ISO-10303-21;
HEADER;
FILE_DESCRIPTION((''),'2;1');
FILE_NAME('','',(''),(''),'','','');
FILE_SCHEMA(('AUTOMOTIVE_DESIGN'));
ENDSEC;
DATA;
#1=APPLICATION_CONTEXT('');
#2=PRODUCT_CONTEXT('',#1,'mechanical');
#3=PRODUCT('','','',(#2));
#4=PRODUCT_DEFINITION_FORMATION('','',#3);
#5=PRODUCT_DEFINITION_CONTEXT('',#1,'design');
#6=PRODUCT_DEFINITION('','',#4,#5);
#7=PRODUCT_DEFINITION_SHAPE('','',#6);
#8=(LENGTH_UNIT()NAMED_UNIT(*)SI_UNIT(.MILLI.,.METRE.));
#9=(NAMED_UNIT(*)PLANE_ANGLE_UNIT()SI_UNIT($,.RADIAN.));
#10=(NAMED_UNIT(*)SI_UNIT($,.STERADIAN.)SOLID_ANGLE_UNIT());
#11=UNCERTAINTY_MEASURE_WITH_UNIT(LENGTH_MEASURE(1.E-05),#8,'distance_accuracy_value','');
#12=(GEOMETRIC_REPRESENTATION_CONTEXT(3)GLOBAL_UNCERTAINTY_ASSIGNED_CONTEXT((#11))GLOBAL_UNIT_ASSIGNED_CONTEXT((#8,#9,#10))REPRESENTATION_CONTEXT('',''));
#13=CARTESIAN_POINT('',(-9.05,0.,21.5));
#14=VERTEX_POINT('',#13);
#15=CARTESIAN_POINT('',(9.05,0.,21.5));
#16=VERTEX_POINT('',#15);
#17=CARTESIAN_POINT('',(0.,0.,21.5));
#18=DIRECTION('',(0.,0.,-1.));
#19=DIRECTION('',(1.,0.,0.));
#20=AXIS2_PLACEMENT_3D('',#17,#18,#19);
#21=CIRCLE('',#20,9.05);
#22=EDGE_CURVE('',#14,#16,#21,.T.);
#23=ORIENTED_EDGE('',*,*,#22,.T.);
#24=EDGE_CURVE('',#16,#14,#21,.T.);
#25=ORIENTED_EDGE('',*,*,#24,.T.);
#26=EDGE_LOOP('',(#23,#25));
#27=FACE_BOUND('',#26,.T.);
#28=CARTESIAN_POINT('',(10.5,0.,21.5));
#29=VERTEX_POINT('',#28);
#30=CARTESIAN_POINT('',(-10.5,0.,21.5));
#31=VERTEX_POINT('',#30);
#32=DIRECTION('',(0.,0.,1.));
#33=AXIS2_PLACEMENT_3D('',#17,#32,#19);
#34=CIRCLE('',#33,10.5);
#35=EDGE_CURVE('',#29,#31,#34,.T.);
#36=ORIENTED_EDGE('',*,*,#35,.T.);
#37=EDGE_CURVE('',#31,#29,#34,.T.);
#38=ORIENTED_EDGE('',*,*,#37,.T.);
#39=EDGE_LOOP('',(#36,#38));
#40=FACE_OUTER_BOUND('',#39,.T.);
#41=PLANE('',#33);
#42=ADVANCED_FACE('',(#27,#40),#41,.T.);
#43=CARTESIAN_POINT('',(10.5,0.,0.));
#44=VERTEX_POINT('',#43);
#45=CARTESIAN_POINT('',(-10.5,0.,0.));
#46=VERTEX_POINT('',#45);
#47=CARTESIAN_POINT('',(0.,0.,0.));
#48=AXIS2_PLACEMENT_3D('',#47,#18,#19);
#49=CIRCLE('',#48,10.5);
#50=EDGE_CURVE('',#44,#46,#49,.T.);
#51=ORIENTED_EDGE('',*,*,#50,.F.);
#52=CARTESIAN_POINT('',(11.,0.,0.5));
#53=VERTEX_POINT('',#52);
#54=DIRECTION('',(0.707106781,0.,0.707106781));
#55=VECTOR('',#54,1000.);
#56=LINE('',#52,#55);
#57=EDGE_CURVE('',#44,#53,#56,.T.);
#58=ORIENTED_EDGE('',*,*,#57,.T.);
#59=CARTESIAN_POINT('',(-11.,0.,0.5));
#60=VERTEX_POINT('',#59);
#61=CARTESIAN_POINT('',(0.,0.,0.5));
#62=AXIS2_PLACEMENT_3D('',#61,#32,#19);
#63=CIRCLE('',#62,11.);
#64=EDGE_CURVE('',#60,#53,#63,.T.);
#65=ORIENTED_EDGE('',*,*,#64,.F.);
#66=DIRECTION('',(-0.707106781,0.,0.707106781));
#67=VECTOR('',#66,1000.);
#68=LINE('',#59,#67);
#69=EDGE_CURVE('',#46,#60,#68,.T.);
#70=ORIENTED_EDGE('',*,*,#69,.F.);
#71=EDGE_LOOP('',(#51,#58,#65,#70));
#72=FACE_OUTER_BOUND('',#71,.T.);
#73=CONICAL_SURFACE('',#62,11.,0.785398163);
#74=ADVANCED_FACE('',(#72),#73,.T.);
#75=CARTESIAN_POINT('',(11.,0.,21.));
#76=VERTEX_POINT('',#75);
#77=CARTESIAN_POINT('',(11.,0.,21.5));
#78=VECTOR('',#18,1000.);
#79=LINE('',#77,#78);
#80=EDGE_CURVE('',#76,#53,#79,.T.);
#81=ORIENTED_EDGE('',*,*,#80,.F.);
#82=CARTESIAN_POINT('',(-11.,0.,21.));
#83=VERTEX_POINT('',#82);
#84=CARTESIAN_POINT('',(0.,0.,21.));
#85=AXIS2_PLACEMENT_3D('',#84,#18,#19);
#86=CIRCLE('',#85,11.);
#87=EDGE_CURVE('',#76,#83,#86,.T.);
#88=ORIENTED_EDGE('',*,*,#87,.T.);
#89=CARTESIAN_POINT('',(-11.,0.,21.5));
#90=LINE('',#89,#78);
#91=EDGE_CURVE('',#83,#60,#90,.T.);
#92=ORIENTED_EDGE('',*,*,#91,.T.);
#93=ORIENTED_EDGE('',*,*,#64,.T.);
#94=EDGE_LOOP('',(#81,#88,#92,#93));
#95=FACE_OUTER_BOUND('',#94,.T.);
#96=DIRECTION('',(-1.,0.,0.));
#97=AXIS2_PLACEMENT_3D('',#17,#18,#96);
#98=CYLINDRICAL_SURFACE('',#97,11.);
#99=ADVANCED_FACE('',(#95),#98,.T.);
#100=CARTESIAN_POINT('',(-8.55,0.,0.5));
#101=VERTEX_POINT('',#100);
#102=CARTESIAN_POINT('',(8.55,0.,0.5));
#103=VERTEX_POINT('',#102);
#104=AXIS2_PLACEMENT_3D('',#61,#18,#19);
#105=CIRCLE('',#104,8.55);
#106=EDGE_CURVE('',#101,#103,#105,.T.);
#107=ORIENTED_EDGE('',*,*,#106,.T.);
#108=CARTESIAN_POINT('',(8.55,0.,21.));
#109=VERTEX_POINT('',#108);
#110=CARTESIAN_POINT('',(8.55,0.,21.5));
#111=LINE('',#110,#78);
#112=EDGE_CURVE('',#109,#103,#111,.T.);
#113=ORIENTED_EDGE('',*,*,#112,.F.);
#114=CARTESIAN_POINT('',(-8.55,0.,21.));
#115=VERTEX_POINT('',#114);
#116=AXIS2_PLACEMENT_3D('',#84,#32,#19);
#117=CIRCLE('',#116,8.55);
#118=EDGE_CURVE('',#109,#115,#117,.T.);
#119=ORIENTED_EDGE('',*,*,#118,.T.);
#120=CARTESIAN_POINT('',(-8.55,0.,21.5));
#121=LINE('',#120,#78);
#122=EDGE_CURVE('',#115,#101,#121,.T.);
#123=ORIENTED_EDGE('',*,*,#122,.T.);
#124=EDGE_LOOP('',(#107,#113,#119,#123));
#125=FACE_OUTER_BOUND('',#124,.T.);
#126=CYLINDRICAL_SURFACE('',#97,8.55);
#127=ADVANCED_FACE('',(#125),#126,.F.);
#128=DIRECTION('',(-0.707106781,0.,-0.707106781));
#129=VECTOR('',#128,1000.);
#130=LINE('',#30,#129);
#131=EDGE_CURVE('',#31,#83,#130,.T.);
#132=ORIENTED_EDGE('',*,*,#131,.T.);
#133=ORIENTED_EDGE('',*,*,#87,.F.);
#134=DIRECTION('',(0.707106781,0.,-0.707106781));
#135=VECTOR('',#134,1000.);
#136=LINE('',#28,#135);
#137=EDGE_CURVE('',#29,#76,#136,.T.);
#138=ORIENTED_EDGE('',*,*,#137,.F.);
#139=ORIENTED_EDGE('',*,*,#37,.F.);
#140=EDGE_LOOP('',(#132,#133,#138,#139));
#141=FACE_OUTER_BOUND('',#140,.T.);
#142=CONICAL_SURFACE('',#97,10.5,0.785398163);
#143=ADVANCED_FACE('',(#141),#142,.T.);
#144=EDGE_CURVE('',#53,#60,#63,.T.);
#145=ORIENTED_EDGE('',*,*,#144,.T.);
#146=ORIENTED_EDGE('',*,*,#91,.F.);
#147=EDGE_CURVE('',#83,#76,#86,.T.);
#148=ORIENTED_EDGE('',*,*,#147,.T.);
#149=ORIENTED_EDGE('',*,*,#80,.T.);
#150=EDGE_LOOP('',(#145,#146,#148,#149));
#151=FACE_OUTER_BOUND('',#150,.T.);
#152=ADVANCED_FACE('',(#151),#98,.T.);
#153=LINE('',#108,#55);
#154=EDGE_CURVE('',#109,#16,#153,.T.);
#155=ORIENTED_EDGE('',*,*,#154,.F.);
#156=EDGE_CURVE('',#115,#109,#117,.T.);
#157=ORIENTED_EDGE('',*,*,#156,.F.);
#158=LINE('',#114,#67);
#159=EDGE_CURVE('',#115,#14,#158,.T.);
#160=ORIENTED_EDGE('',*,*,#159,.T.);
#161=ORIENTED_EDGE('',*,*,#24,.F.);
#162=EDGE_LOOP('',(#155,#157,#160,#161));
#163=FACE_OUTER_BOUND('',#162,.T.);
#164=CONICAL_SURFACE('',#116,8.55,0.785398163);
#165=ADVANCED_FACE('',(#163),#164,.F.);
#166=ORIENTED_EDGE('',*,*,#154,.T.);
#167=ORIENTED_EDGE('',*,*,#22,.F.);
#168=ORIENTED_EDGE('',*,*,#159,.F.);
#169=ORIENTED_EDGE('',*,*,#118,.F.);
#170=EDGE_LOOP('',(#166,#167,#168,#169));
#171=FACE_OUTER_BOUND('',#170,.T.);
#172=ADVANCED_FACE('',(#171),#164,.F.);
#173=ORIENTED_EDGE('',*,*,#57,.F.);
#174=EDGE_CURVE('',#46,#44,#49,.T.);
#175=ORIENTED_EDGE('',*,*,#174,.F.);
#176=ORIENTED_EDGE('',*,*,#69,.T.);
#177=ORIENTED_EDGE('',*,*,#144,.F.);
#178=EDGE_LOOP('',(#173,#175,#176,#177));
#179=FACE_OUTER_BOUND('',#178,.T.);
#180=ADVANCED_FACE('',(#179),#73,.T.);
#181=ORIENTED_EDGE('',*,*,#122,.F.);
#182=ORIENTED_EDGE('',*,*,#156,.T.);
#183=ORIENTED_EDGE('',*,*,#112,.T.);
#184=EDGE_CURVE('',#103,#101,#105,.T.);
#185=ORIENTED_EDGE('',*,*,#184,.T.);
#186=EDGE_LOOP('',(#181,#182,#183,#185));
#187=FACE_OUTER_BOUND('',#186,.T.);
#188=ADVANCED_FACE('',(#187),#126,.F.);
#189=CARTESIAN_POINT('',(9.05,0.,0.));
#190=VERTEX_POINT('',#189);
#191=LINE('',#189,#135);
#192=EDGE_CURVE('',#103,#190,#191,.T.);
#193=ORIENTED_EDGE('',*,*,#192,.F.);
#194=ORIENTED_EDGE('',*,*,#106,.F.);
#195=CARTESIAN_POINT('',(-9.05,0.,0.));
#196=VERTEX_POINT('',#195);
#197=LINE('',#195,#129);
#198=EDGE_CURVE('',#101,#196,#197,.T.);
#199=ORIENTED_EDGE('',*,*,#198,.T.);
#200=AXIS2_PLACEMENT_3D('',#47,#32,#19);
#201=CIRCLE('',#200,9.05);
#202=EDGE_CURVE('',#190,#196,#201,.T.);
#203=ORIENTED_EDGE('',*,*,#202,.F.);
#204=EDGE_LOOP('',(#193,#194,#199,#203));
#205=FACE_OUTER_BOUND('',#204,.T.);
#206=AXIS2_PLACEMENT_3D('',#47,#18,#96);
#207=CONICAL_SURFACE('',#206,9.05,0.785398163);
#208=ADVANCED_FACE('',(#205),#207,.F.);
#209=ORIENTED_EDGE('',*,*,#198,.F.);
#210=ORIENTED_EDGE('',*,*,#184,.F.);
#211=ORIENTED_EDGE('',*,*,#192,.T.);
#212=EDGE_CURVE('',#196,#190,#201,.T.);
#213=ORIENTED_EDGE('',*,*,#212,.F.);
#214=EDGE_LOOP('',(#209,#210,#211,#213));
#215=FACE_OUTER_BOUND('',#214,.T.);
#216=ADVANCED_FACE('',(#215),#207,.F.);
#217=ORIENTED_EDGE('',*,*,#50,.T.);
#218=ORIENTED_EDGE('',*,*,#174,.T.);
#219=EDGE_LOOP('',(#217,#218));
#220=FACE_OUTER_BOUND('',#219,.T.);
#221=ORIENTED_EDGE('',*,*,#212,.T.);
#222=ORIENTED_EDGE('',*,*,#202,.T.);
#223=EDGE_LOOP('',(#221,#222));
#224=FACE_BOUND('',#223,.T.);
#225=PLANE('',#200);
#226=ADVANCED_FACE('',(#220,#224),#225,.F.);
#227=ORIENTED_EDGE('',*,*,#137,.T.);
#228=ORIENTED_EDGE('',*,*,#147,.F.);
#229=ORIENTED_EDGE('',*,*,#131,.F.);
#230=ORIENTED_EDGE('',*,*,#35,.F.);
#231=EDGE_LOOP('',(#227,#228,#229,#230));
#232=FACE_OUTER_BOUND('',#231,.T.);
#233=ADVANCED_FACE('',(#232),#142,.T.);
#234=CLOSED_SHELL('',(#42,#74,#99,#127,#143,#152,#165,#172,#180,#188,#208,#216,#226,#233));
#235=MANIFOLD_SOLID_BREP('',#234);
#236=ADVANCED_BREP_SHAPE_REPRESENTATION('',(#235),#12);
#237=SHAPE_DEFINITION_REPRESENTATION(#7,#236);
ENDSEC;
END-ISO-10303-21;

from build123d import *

# Parameters (mm, degrees)
SKETCH_1_R      = 11
SKETCH_1_R_2    = 8.55
EXTRUDE_1_DEPTH = 21.5
CHAMFER_1_SIZE  = 0.5


with BuildPart() as part:
    # 草图1 → 凸台-拉伸1 (new body)
    with BuildSketch(Plane.XY):
        Circle(SKETCH_1_R)
        Circle(SKETCH_1_R_2, mode=Mode.SUBTRACT)
    extrude(amount=EXTRUDE_1_DEPTH)

    # 倒角1
    chamfer_1_edges = [part.edges().sort_by_distance(p)[0] for p in [
        (-11, 0, 0),
        (-11, 0, 21.5),
        (-8.55, 0, 0),
        (-8.55, 0, 21.5),
    ]]
    chamfer(chamfer_1_edges, length=CHAMFER_1_SIZE)


solid = part.part
